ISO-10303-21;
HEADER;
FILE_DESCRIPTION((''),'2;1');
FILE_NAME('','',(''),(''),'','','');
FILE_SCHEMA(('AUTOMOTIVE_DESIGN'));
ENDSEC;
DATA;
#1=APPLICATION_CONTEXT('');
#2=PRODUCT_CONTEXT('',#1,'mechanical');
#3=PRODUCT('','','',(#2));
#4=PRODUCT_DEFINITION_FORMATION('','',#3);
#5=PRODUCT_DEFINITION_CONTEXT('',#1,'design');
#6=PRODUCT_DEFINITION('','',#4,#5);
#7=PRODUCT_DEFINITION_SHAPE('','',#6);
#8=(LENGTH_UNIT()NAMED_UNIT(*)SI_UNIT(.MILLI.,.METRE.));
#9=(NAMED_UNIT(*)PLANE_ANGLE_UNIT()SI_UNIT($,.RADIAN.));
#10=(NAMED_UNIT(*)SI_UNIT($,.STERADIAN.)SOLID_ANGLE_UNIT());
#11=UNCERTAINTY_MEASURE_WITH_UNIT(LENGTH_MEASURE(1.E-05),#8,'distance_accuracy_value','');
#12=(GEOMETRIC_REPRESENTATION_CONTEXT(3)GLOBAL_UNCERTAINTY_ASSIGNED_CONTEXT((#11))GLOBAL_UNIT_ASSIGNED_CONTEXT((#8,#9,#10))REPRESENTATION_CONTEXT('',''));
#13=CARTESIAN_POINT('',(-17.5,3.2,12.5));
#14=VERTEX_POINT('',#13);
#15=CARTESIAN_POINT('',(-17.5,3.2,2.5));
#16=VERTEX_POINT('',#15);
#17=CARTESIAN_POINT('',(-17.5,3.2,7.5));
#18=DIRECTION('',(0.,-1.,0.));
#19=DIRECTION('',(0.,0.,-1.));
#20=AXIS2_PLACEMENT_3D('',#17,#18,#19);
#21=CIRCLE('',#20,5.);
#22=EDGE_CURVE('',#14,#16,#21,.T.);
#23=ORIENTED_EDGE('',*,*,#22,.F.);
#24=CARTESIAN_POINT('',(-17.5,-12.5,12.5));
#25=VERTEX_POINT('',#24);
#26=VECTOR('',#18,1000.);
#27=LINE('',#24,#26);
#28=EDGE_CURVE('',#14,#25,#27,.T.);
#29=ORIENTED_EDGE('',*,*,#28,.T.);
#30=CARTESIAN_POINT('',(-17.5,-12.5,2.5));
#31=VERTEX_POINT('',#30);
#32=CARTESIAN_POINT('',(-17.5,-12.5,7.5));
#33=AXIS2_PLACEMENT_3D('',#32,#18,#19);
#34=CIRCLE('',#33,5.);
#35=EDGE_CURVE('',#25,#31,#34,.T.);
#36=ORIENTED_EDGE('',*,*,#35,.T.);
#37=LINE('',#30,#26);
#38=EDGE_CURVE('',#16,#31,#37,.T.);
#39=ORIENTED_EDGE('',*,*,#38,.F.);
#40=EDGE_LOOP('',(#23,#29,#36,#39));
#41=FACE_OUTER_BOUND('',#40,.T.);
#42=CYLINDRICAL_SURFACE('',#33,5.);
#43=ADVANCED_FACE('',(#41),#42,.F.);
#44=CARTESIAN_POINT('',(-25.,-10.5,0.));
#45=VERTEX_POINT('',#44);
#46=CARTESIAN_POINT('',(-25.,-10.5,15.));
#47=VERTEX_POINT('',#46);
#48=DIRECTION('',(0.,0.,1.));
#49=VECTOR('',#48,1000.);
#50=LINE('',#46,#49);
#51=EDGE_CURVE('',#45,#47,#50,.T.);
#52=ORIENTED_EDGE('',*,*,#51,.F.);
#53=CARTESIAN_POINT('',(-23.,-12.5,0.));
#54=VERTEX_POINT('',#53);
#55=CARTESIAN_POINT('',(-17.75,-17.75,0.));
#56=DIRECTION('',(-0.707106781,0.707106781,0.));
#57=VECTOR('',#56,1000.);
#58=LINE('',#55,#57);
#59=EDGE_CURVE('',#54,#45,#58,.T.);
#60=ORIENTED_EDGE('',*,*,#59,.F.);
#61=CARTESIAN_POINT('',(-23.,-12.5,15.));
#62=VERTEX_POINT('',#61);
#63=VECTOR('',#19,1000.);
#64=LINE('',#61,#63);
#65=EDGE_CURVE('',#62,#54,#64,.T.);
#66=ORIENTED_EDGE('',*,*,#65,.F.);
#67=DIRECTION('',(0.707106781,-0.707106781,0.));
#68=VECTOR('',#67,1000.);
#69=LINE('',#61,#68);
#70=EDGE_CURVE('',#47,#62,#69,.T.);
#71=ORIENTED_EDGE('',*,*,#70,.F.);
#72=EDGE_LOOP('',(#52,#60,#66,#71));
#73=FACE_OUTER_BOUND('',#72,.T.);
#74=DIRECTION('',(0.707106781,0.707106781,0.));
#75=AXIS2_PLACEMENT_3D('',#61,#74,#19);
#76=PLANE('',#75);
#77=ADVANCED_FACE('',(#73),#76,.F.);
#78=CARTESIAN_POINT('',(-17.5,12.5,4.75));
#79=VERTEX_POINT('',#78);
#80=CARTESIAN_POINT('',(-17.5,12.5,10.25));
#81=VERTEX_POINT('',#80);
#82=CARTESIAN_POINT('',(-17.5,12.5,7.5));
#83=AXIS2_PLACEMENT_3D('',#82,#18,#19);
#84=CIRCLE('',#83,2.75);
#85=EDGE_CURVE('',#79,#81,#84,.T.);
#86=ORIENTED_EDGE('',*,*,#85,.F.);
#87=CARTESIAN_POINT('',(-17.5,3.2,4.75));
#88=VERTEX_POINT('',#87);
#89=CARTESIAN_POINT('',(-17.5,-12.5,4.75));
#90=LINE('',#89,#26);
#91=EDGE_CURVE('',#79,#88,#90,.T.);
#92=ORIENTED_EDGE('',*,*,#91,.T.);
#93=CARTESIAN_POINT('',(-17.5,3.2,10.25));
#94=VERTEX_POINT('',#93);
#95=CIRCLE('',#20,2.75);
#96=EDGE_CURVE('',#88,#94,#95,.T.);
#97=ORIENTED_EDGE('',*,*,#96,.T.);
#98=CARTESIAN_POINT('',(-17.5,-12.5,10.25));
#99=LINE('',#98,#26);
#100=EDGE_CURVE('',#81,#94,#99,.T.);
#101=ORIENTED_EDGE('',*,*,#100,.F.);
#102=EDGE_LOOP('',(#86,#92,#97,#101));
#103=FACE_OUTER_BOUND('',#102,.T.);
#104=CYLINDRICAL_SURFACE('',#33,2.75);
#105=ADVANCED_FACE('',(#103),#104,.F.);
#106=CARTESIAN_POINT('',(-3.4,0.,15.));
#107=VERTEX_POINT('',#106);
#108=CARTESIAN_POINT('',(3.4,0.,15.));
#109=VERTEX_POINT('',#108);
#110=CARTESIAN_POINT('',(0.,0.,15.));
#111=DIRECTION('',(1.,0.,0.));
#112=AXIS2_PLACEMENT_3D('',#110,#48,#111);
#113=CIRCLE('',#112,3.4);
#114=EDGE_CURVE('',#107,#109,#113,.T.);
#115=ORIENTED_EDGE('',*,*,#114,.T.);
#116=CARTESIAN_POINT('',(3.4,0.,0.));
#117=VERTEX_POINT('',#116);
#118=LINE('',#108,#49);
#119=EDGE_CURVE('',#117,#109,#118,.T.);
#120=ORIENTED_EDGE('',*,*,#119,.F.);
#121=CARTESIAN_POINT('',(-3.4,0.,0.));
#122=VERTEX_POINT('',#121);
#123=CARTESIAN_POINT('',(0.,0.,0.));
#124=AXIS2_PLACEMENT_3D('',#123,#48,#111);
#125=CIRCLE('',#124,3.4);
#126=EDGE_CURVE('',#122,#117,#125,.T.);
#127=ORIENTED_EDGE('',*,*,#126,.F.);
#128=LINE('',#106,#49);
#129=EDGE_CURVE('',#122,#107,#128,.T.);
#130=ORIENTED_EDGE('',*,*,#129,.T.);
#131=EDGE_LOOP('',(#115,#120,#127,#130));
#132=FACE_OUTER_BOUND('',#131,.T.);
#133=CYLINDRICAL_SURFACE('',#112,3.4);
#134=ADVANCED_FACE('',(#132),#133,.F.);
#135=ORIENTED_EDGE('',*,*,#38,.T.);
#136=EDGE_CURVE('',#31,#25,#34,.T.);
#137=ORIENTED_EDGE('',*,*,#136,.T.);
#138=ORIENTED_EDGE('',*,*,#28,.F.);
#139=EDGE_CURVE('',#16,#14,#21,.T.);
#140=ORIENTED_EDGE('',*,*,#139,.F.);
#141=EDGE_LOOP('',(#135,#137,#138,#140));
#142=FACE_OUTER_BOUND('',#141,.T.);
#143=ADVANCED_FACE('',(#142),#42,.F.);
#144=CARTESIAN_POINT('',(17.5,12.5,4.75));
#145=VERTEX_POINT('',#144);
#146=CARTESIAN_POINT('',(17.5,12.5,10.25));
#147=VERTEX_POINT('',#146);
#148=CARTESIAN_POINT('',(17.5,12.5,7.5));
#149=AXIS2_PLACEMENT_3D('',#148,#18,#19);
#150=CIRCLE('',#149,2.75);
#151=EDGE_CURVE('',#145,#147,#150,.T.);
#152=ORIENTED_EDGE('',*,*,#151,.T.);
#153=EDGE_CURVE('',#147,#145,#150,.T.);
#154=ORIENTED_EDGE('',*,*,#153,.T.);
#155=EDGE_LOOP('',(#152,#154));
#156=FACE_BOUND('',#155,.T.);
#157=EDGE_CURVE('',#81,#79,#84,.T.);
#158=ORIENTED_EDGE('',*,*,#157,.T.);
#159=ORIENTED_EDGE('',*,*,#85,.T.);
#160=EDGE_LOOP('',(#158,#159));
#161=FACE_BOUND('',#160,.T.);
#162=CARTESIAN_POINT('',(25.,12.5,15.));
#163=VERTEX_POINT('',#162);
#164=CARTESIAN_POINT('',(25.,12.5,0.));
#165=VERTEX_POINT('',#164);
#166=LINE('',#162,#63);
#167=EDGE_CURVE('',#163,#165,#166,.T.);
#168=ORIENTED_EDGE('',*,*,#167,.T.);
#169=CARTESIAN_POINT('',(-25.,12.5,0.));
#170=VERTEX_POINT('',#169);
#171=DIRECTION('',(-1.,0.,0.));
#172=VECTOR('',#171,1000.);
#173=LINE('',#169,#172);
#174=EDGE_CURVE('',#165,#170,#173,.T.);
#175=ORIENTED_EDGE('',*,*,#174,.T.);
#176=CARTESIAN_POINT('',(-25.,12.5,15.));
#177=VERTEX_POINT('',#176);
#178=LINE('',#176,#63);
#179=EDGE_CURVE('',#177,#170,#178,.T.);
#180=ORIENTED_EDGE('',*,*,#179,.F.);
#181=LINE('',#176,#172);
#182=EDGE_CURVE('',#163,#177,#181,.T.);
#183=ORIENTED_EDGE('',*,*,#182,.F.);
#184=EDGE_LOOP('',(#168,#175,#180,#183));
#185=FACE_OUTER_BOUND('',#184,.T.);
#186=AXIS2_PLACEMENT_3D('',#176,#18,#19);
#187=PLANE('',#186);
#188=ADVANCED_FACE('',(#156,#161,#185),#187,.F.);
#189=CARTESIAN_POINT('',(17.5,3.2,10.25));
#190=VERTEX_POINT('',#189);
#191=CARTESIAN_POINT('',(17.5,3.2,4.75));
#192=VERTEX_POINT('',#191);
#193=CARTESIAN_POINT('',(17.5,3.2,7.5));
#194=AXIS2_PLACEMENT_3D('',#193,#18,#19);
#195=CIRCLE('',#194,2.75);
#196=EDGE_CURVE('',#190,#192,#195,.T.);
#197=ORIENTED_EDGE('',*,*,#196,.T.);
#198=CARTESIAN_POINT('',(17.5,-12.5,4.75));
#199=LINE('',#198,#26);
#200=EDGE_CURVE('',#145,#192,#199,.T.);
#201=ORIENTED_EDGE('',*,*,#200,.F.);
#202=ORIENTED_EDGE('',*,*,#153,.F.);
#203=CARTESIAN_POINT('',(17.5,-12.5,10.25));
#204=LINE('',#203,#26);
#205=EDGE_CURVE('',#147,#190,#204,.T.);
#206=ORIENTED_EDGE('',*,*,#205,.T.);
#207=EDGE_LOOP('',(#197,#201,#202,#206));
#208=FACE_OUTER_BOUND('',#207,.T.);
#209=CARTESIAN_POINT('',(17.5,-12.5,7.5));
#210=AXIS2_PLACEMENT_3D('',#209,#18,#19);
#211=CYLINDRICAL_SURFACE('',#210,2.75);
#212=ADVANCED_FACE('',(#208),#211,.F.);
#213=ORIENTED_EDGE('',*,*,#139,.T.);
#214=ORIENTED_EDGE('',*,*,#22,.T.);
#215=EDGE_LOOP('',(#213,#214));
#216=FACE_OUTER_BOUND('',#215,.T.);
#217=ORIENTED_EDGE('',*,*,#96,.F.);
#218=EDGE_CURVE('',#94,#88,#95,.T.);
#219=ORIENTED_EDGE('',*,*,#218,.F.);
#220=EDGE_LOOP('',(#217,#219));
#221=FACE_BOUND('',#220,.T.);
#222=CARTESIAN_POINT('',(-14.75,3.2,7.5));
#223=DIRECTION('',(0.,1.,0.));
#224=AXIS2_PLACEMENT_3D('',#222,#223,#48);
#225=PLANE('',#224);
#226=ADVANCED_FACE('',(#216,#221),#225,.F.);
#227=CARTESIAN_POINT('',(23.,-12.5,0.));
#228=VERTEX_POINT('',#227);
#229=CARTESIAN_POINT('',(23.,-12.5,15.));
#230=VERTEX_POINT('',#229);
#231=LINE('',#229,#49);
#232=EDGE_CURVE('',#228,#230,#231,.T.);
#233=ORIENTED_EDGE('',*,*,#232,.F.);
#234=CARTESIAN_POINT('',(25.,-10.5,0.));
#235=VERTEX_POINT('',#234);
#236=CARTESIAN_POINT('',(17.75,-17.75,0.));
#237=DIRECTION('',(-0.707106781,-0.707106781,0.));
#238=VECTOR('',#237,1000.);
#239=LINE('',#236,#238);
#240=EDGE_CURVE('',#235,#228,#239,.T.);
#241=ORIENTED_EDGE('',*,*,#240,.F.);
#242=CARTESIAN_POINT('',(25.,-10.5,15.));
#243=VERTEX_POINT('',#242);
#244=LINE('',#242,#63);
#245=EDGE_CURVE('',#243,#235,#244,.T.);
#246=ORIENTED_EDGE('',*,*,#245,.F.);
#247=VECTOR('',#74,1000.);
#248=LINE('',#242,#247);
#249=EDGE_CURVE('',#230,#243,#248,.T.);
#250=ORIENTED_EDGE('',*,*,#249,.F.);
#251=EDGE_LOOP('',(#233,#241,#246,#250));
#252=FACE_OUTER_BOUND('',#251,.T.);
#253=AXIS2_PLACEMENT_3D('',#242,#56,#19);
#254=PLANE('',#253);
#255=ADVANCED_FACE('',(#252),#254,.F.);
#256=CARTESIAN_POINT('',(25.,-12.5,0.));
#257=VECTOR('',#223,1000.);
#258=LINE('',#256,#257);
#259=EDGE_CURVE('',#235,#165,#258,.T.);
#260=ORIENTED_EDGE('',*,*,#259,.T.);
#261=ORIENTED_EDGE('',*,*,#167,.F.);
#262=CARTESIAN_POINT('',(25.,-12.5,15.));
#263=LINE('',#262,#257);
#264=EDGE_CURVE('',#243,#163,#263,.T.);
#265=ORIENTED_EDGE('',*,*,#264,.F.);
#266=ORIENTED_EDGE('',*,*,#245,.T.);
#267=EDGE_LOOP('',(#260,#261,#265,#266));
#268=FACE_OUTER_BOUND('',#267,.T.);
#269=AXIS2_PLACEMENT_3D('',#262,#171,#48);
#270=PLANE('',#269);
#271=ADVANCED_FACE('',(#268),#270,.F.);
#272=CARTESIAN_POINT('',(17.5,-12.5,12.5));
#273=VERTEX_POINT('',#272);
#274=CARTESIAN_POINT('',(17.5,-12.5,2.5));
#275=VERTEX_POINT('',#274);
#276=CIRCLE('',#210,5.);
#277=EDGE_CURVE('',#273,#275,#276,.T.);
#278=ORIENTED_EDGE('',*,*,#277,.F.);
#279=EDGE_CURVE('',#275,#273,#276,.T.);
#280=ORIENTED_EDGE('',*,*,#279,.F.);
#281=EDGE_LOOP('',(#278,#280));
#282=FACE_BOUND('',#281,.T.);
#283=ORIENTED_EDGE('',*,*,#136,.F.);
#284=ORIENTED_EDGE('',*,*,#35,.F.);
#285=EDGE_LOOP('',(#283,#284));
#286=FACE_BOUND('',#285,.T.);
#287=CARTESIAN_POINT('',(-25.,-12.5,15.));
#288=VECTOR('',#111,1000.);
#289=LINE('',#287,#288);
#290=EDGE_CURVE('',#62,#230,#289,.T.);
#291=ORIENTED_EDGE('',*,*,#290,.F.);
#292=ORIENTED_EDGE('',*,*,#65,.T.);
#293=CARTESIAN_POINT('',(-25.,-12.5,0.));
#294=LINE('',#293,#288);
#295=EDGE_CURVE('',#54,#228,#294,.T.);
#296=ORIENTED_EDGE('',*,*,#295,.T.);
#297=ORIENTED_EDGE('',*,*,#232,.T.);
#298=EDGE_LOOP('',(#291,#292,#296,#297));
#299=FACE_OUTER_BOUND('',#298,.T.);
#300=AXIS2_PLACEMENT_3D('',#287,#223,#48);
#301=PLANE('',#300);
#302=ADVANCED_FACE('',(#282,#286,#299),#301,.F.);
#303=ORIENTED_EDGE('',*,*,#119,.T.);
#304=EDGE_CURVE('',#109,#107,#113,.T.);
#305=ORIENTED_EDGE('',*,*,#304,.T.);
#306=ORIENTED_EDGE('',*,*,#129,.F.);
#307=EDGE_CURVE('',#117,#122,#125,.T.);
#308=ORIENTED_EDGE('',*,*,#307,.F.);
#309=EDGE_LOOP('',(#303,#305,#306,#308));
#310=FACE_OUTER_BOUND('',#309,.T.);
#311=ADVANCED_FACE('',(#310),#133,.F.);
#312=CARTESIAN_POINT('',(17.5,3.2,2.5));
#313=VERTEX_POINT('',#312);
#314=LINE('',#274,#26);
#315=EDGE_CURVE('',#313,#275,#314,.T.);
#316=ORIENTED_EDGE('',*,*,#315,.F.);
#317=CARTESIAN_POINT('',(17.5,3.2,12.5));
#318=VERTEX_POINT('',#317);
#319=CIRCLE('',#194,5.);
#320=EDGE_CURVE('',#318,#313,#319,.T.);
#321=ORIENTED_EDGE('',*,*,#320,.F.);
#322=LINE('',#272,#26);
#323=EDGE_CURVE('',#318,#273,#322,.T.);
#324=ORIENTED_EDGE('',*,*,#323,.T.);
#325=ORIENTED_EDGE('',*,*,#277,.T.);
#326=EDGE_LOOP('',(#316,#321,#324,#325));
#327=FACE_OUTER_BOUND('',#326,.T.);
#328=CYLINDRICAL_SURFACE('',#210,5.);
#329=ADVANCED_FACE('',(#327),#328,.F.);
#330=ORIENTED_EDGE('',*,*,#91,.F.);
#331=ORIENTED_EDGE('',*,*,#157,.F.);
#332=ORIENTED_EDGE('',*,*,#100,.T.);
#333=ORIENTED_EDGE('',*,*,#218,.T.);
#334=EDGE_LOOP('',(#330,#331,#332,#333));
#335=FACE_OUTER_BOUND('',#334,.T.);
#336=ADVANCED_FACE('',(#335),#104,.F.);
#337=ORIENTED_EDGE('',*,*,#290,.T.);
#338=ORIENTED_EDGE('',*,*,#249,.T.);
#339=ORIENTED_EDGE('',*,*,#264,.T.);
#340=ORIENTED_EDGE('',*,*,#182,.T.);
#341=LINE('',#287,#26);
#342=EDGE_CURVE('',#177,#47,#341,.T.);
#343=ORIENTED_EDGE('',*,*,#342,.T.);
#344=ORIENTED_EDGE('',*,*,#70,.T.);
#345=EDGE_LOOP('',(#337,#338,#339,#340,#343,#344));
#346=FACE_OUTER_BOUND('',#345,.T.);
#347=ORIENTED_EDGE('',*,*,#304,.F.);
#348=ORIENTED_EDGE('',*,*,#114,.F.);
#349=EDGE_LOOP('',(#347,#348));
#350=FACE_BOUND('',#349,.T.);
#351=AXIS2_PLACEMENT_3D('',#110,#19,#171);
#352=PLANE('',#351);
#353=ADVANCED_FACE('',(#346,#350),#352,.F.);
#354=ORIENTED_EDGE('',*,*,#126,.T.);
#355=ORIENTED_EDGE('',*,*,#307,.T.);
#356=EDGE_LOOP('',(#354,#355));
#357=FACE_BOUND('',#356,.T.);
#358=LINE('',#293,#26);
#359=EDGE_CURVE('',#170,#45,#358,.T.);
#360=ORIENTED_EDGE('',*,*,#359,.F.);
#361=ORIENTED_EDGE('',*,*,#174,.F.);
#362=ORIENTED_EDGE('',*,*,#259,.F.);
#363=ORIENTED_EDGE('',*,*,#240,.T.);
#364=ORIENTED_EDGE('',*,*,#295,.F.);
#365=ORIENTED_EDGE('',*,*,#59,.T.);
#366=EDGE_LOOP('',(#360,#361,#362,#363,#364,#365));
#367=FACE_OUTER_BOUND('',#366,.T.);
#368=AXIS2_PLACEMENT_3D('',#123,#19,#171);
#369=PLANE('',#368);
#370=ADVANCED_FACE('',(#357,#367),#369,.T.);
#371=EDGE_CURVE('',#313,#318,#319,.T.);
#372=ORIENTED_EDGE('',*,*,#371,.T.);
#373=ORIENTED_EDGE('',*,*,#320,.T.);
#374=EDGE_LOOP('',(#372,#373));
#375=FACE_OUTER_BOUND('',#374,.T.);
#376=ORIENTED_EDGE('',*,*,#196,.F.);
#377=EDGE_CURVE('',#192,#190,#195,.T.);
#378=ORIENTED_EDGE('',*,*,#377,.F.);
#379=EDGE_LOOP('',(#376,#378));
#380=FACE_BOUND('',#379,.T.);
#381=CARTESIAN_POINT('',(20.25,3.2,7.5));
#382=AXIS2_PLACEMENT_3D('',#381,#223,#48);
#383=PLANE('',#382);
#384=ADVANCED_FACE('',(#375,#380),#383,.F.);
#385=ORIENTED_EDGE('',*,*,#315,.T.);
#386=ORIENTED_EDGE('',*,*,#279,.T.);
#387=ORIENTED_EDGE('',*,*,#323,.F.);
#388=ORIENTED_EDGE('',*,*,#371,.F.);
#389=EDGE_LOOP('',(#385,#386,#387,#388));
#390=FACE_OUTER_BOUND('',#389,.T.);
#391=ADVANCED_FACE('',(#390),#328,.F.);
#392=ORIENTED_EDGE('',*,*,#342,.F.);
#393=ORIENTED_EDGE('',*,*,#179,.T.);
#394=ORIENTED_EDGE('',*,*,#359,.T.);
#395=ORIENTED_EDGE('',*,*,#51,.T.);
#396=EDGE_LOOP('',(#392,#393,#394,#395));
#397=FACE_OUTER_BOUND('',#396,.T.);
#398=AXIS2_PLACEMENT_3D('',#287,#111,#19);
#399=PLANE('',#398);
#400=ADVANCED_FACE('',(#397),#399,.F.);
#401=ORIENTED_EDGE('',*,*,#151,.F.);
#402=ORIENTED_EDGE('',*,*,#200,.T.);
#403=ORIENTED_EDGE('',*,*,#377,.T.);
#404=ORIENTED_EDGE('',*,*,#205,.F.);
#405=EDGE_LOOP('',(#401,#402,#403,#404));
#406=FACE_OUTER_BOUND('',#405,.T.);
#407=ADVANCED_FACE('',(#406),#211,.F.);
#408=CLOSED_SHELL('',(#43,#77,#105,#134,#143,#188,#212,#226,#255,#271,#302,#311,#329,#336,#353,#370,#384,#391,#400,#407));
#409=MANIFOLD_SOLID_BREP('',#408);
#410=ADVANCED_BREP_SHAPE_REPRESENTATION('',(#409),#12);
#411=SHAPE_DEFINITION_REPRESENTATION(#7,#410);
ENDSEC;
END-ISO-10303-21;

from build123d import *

# Parameters (mm, degrees)
SKETCH_1_W                   = 50
SKETCH_1_H                   = 25
EXTRUDE_1_DEPTH              = 15
CHAMFER_1_SIZE               = 2
HOLE_WIZARD_M5_1_D           = 5.5
HOLE_WIZARD_M5_1_CBORE_D     = 10
HOLE_WIZARD_M5_1_CBORE_DEPTH = 15.7
HOLE_WIZARD_M8_1_D           = 6.8


with BuildPart() as part:
    # 草图1 → 凸台-拉伸1 (new body)
    with BuildSketch(Plane.XY):
        Rectangle(SKETCH_1_W, SKETCH_1_H)
    extrude(amount=EXTRUDE_1_DEPTH)

    # 倒角1
    chamfer_1_edges = [part.edges().sort_by_distance(p)[0] for p in [
        (25, -12.5, 7.5),
        (-25, -12.5, 7.5),
    ]]
    chamfer(chamfer_1_edges, length=CHAMFER_1_SIZE)

    # M5 六角圆柱头螺钉的柱形沉头孔1 (through all)
    with Locations(Plane(origin=(0, -12.5, 0), x_dir=(-1, 0, 0), z_dir=(0, -1, 0))):
        with Locations((-17.5, -7.5), (17.5, -7.5)):
            CounterBoreHole(HOLE_WIZARD_M5_1_D / 2, HOLE_WIZARD_M5_1_CBORE_D / 2, HOLE_WIZARD_M5_1_CBORE_DEPTH)

    # M8 螺纹孔1 (through all)
    with Locations(Plane.XY.offset(15)):
        with Locations((0, 0)):
            Hole(HOLE_WIZARD_M8_1_D / 2)


solid = part.part
